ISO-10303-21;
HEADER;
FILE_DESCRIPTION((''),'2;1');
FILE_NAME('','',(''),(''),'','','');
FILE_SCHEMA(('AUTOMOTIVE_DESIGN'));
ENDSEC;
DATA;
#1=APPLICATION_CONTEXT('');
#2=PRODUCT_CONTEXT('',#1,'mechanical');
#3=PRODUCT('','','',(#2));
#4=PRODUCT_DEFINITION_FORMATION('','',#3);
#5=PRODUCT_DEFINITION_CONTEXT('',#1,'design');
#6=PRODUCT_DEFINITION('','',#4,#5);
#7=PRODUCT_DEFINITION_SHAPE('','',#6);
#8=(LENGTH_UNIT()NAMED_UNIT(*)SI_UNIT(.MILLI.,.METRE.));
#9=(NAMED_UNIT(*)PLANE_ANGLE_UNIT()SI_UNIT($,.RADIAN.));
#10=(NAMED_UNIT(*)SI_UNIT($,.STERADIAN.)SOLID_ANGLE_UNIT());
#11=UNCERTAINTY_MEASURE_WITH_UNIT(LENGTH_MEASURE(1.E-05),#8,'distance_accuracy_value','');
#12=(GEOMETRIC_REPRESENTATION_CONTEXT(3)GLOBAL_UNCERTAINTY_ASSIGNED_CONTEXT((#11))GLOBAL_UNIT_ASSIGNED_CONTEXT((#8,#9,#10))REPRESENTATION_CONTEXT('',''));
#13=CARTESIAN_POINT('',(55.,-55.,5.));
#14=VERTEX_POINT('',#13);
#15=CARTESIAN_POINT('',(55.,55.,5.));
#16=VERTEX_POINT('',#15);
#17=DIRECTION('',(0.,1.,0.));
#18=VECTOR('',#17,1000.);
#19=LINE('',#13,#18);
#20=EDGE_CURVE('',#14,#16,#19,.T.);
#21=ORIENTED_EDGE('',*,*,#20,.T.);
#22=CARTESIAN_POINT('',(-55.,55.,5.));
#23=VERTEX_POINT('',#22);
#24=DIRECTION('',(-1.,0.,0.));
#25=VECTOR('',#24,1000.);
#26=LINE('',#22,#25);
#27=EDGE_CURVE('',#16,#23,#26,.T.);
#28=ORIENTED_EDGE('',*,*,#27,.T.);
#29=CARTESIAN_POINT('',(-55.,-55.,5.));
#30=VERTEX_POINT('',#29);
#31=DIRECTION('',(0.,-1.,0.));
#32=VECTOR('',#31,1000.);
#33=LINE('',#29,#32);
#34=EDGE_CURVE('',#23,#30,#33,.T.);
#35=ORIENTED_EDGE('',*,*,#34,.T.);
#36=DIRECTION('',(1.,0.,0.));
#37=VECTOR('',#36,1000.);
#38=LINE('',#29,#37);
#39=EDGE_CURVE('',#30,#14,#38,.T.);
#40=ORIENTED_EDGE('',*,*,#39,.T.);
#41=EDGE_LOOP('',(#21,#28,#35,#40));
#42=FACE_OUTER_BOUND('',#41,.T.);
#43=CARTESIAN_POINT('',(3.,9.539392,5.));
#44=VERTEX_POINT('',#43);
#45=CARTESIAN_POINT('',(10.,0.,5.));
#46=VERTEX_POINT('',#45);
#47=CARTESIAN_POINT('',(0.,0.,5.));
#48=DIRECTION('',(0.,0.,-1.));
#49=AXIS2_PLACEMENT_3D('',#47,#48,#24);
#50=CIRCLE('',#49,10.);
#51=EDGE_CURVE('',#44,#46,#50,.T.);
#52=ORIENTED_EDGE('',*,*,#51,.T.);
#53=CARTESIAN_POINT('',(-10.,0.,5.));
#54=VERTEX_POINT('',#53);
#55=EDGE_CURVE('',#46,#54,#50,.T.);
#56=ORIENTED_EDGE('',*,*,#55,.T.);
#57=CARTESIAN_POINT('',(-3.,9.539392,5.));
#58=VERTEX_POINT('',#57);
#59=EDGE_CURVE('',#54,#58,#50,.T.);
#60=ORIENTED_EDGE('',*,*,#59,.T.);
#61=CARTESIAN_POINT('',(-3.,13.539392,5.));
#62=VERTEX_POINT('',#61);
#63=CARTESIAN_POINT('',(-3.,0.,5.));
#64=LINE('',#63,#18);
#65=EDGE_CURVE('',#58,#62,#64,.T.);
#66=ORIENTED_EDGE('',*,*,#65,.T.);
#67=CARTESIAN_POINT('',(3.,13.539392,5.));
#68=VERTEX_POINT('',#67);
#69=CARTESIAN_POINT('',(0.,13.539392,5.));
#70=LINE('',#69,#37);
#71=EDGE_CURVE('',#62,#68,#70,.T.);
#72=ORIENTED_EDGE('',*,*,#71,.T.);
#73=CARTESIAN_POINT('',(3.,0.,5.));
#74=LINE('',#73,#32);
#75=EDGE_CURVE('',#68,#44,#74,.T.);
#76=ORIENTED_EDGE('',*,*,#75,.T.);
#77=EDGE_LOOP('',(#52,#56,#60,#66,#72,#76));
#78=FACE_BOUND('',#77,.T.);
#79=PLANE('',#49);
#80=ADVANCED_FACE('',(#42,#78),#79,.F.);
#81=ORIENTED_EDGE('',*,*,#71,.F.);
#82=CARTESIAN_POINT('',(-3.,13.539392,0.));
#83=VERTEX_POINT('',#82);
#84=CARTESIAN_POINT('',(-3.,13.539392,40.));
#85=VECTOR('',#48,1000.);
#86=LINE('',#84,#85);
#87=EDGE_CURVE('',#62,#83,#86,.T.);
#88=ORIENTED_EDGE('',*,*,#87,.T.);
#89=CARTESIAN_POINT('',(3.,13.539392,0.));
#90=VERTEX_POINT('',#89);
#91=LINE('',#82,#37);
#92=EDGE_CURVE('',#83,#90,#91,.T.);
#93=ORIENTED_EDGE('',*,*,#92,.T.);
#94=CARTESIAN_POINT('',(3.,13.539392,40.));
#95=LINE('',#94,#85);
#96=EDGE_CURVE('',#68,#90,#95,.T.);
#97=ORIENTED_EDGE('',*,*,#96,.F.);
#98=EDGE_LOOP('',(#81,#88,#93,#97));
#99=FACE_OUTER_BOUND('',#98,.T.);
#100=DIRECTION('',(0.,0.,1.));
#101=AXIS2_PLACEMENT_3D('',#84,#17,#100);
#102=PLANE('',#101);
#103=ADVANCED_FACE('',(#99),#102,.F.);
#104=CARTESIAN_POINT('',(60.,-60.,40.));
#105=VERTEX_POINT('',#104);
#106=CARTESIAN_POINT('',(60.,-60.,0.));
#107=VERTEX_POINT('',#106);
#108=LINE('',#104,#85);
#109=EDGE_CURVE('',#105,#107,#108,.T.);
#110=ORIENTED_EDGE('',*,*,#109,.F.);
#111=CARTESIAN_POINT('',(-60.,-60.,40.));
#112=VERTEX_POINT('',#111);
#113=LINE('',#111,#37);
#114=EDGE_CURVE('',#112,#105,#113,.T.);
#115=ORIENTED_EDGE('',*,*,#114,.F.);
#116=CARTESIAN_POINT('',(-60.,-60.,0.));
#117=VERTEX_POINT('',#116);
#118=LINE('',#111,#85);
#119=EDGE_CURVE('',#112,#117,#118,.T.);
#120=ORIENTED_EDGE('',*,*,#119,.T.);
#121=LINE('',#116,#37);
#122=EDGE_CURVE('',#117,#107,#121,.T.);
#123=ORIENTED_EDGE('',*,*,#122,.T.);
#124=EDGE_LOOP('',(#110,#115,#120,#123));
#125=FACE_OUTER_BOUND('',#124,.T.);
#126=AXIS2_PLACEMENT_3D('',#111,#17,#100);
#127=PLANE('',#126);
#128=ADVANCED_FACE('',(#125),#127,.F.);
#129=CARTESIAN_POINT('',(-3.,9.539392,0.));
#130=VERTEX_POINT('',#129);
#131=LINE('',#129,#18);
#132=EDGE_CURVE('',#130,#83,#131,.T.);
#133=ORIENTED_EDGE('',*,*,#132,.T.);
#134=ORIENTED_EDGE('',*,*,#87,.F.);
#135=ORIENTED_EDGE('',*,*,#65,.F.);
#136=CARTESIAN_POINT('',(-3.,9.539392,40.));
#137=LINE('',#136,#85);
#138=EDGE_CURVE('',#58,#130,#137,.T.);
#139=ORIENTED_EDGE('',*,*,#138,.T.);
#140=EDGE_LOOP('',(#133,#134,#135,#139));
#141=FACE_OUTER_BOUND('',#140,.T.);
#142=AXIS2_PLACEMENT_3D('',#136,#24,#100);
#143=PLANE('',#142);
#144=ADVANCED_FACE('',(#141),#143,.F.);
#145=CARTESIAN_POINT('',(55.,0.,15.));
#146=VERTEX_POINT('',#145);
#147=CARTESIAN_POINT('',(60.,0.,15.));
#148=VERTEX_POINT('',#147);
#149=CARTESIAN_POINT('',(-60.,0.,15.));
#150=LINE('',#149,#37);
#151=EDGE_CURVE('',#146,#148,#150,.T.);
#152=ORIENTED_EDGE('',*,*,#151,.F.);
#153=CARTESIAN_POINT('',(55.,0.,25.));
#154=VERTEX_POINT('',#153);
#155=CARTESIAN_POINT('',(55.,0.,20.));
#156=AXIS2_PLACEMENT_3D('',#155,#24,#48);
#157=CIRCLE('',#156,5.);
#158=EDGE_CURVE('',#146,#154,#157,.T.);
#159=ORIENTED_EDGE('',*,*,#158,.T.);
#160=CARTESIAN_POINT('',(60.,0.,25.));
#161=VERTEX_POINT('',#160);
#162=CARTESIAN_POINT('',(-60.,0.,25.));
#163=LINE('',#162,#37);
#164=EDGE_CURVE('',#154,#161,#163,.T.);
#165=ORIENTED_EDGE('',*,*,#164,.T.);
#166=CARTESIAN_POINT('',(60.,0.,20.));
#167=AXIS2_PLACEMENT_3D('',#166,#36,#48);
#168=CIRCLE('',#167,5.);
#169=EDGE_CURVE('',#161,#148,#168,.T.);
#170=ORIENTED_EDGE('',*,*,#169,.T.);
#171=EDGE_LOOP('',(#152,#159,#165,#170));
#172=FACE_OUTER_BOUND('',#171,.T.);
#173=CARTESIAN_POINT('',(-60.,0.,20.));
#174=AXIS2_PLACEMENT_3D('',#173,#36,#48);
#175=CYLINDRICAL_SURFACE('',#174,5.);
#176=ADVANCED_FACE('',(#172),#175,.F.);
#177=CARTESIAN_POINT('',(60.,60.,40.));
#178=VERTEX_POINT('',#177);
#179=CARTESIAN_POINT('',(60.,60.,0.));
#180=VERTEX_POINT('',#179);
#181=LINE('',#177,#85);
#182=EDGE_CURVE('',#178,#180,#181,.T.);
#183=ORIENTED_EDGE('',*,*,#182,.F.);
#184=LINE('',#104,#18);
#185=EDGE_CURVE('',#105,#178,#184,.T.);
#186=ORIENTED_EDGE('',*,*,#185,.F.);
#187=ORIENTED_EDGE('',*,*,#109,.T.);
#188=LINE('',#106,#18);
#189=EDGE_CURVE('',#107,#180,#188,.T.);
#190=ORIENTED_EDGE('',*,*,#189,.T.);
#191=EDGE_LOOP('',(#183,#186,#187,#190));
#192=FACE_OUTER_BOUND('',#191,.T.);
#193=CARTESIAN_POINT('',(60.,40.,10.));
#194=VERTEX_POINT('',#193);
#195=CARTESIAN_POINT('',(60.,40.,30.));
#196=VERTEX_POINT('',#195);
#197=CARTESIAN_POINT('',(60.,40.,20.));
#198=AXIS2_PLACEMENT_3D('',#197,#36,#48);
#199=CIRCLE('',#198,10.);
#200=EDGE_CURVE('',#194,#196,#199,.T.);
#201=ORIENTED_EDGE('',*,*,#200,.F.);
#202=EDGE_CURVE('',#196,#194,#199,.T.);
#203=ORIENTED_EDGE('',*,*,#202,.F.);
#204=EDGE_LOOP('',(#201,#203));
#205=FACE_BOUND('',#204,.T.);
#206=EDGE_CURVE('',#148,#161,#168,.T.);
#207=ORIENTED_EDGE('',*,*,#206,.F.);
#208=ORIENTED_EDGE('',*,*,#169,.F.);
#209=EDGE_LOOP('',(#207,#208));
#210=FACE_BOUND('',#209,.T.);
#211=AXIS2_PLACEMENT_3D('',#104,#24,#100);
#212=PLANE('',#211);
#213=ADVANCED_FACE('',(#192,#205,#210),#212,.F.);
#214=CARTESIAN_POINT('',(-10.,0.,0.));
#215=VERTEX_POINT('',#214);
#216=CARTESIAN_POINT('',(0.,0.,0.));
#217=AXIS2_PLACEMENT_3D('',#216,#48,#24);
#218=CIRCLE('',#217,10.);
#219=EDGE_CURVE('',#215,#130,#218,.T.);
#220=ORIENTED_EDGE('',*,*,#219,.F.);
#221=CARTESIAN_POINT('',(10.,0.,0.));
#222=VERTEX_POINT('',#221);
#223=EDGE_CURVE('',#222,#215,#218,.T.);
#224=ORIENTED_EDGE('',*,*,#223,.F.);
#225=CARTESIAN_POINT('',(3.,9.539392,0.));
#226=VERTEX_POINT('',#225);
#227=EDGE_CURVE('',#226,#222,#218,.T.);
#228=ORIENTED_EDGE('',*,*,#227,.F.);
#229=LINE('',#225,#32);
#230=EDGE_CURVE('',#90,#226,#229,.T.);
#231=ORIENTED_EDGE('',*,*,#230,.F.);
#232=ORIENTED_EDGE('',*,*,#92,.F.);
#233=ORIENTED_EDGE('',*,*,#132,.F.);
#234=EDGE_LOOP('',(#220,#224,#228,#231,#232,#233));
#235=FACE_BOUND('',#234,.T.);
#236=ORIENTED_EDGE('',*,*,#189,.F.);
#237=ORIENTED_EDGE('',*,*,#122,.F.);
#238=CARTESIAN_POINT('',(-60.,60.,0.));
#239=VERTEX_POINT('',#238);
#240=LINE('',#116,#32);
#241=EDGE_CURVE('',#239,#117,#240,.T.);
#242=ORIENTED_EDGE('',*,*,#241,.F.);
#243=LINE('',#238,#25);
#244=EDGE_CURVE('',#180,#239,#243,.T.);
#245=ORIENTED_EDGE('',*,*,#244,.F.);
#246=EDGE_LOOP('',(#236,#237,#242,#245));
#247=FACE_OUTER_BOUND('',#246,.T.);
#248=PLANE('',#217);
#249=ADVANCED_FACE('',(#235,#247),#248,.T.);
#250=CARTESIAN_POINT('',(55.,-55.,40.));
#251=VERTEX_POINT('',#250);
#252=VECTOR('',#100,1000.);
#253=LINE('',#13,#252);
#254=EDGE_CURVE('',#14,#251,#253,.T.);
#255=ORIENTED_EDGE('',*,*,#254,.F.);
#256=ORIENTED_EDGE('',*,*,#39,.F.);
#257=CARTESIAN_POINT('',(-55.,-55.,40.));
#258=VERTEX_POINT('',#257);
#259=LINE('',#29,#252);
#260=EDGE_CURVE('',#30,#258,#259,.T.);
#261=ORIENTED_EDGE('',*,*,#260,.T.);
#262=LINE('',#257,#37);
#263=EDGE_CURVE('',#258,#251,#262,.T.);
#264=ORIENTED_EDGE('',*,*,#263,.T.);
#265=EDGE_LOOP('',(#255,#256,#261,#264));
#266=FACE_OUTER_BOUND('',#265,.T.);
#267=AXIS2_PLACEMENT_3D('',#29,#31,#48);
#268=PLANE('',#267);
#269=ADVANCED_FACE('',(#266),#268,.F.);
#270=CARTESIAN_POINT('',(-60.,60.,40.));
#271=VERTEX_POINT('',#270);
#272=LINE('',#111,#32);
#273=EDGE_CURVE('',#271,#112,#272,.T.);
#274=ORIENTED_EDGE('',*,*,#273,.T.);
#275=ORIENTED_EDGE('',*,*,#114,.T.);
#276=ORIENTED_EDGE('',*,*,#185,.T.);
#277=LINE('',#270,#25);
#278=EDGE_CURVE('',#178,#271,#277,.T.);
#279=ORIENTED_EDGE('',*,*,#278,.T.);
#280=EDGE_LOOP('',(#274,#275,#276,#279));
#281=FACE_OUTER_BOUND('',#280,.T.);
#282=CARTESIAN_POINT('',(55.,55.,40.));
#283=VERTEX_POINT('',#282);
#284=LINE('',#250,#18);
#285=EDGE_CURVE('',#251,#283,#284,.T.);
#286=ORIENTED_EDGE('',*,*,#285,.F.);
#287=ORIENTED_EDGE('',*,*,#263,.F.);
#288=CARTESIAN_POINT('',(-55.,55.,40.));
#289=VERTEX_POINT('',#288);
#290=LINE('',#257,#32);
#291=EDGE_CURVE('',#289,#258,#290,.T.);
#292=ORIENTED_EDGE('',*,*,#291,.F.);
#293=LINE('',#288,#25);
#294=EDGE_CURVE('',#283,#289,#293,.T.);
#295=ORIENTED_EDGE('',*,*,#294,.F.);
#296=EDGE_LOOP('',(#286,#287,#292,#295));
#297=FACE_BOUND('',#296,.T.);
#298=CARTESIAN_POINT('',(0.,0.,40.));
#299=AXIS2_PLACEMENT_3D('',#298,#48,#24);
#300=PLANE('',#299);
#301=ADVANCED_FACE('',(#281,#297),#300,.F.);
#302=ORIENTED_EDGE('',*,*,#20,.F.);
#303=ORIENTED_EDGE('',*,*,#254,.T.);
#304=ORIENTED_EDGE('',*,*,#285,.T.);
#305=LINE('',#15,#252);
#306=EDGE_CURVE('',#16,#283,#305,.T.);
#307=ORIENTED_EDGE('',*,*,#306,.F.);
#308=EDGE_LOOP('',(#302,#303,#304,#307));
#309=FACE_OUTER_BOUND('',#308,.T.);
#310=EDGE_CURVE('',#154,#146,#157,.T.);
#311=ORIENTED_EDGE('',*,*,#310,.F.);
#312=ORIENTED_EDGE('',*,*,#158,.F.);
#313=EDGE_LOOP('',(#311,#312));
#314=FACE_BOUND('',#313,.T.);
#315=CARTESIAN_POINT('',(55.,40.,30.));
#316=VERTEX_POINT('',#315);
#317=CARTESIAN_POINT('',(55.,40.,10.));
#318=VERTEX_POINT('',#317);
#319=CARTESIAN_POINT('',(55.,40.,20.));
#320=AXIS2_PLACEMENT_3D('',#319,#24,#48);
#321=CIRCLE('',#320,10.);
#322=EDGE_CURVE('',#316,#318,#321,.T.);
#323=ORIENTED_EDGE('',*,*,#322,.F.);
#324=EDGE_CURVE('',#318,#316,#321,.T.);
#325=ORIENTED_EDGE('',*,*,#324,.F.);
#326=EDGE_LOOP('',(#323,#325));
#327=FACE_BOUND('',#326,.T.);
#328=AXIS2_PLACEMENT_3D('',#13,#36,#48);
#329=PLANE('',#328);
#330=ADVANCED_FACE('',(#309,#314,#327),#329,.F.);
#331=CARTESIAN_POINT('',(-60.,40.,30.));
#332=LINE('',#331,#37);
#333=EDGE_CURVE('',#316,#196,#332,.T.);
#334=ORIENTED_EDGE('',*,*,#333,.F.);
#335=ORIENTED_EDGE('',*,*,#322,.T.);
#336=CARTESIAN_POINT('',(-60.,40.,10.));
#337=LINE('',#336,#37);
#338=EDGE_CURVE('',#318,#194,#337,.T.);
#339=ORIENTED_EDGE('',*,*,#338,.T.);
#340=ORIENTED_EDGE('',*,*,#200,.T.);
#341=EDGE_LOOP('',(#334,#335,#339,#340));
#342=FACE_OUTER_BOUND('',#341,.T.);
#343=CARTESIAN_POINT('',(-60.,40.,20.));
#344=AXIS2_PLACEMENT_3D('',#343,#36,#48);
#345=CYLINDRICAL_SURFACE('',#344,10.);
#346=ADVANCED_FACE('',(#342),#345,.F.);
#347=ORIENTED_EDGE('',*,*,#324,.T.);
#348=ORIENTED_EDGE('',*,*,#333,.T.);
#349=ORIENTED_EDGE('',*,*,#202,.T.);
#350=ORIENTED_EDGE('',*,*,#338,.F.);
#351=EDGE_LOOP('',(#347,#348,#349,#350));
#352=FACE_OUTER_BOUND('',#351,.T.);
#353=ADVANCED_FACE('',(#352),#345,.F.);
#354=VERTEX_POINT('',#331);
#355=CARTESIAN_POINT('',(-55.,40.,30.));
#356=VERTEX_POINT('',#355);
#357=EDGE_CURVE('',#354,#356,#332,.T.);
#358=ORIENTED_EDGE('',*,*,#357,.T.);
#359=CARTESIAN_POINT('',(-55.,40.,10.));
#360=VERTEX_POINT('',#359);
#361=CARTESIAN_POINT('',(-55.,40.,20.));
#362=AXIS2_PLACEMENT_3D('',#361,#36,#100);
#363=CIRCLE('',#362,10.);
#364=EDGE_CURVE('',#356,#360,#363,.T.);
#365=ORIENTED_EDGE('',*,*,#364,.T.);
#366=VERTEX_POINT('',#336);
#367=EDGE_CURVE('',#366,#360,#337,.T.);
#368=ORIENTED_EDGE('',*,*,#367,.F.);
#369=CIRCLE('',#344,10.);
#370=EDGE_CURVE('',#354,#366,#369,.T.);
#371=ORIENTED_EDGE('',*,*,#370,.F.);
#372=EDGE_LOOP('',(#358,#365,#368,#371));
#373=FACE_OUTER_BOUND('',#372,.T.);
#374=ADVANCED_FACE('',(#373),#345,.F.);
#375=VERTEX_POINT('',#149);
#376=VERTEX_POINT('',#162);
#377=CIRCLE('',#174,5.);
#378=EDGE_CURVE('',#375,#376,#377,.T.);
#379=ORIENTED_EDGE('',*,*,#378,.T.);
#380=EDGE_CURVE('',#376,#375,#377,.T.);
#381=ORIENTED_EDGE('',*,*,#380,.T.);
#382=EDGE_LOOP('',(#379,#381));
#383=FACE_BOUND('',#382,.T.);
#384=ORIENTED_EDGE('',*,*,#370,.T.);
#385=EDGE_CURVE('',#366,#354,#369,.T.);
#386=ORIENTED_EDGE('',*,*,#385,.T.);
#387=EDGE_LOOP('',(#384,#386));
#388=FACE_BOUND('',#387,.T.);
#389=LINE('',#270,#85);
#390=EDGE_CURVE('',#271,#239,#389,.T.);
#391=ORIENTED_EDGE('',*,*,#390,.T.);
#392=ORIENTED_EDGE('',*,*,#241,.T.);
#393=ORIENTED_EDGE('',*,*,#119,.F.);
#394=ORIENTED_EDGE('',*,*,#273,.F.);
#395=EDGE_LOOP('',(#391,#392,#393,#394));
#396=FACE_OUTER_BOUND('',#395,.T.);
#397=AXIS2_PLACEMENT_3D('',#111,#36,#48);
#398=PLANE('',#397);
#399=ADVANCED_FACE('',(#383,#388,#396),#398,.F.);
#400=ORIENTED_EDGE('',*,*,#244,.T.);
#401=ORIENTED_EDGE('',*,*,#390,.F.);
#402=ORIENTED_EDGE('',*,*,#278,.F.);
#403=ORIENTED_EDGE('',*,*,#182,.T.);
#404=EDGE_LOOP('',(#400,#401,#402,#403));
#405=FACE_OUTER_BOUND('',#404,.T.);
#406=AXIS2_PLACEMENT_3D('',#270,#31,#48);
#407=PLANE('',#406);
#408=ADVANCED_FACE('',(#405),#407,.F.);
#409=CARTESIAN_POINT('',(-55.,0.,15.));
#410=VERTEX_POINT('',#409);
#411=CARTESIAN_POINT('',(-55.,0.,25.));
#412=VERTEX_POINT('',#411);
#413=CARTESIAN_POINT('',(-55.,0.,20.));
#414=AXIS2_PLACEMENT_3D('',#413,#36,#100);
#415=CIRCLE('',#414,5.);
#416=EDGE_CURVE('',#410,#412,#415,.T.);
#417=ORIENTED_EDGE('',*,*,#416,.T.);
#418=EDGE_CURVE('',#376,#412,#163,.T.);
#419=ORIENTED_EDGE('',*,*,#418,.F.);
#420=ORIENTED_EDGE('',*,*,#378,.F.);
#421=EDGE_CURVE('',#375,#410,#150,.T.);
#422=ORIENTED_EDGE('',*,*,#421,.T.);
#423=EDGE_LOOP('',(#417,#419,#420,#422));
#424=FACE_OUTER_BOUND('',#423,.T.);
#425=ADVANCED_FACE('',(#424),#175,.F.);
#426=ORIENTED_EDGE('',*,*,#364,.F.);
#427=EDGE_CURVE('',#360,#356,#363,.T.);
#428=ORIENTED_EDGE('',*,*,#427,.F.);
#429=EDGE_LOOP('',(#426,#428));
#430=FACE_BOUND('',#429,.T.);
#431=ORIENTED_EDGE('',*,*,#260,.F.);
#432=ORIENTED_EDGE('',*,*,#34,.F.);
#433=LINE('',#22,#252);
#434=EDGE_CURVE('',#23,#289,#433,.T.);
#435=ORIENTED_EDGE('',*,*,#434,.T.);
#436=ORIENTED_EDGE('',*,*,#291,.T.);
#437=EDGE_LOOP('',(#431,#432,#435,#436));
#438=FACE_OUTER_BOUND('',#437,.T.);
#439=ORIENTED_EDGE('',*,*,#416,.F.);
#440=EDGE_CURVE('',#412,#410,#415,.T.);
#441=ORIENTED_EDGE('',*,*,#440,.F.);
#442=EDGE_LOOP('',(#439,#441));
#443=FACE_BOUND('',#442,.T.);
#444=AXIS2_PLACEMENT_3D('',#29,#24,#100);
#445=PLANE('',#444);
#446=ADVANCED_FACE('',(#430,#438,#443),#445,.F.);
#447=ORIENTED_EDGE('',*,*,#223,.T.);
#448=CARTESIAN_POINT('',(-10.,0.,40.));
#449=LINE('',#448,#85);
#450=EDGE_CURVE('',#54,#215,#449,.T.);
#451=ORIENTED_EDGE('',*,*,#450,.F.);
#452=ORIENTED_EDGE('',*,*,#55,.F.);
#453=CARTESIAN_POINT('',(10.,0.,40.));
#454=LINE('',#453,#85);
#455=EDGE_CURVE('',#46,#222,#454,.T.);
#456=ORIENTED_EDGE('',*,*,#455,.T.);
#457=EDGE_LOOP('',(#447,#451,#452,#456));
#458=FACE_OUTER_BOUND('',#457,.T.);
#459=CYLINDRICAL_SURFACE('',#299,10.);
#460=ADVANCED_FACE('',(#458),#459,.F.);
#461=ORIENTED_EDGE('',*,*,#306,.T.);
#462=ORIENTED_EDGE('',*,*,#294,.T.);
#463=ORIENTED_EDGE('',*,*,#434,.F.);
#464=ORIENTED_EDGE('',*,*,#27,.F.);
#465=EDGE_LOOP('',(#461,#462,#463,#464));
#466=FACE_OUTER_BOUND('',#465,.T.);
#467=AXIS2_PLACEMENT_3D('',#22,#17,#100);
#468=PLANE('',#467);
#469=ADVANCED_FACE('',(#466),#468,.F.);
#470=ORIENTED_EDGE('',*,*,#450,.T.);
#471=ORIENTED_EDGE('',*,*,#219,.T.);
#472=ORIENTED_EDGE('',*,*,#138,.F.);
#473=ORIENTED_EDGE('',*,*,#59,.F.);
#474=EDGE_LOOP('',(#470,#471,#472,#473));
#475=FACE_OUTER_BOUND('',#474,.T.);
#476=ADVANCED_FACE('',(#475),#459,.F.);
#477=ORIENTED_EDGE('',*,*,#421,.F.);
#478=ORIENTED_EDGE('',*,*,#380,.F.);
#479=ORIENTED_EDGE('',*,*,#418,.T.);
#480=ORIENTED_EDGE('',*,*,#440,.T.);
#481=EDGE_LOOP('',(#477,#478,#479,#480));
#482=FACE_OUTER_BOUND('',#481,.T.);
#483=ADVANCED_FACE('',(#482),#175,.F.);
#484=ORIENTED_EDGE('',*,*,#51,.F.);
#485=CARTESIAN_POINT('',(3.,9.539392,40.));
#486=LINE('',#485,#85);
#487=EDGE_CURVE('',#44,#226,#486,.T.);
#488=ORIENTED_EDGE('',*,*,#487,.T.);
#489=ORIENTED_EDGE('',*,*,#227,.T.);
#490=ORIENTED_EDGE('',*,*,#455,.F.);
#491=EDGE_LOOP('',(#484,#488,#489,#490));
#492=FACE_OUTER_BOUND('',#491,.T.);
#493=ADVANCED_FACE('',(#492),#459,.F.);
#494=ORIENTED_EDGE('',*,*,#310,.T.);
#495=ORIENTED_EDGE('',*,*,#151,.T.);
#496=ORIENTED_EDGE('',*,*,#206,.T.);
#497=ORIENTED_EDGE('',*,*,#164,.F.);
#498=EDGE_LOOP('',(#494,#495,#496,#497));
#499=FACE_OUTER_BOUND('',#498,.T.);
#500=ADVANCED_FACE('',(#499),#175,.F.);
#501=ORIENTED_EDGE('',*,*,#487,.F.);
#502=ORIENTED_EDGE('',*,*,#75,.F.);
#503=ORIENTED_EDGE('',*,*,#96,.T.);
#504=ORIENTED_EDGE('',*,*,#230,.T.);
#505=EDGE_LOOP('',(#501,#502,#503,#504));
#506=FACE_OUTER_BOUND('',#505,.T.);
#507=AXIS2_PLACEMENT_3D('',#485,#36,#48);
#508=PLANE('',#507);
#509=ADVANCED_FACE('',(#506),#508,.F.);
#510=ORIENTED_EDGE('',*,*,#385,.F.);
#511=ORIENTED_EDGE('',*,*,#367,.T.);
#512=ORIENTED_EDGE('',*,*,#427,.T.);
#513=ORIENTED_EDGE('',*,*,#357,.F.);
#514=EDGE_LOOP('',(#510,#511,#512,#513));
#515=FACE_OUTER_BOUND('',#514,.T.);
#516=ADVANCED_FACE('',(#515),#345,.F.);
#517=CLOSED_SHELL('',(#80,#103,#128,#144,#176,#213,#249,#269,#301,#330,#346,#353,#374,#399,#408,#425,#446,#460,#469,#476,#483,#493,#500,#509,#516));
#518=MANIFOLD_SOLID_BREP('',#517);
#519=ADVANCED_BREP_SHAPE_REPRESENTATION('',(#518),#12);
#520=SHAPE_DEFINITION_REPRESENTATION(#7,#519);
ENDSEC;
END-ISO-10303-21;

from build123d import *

# Parameters (mm, degrees)
SKETCH_1_W          = 120
SKETCH_1_H          = 120
EXTRUDE_1_DEPTH     = 40
SKETCH_3_R          = 10
SKETCH_3_R_2        = 5
CUT_EXTRUDE_1_DEPTH = 141
SKETCH_4_W          = 110
SKETCH_4_H          = 110
CUT_EXTRUDE_3_DEPTH = 35
CUT_EXTRUDE_4_DEPTH = 94.808315196


with BuildPart() as part:
    # 草图1 → 凸台-拉伸1 (new body)
    with BuildSketch(Plane.XY):
        Rectangle(SKETCH_1_W, SKETCH_1_H)
    extrude(amount=EXTRUDE_1_DEPTH)

    # 草图3 → 切除-拉伸1 (cut, through all)
    with BuildSketch(Plane(origin=(60, 0, 0), x_dir=(0, 0, -1), z_dir=(1, 0, 0))):
        with Locations((-20, 40)):
            Circle(SKETCH_3_R)
        with Locations((-20, 0)):
            Circle(SKETCH_3_R_2)
    extrude(amount=-CUT_EXTRUDE_1_DEPTH, mode=Mode.SUBTRACT)

    # 草图4 → 切除-拉伸3 (cut)
    with BuildSketch(Plane.XY.offset(40)):
        Rectangle(SKETCH_4_W, SKETCH_4_H)
    extrude(amount=-CUT_EXTRUDE_3_DEPTH, mode=Mode.SUBTRACT)

    # 草图5 → 切除-拉伸4 (cut, through all)
    with BuildSketch(Plane(origin=(0, 0, 0), x_dir=(-1, 0, 0), z_dir=(0, 0, -1))):
        with BuildLine():
            Line((-3, 9.539392014), (-3, 13.539392014))
            Line((-3, 13.539392014), (3, 13.539392014))
            Line((3, 13.539392014), (3, 9.539392014))
            ThreePointArc((3, 9.539392014), (0, -10), (-3, 9.539392014))
        make_face()
    extrude(amount=-CUT_EXTRUDE_4_DEPTH, mode=Mode.SUBTRACT)


solid = part.part
